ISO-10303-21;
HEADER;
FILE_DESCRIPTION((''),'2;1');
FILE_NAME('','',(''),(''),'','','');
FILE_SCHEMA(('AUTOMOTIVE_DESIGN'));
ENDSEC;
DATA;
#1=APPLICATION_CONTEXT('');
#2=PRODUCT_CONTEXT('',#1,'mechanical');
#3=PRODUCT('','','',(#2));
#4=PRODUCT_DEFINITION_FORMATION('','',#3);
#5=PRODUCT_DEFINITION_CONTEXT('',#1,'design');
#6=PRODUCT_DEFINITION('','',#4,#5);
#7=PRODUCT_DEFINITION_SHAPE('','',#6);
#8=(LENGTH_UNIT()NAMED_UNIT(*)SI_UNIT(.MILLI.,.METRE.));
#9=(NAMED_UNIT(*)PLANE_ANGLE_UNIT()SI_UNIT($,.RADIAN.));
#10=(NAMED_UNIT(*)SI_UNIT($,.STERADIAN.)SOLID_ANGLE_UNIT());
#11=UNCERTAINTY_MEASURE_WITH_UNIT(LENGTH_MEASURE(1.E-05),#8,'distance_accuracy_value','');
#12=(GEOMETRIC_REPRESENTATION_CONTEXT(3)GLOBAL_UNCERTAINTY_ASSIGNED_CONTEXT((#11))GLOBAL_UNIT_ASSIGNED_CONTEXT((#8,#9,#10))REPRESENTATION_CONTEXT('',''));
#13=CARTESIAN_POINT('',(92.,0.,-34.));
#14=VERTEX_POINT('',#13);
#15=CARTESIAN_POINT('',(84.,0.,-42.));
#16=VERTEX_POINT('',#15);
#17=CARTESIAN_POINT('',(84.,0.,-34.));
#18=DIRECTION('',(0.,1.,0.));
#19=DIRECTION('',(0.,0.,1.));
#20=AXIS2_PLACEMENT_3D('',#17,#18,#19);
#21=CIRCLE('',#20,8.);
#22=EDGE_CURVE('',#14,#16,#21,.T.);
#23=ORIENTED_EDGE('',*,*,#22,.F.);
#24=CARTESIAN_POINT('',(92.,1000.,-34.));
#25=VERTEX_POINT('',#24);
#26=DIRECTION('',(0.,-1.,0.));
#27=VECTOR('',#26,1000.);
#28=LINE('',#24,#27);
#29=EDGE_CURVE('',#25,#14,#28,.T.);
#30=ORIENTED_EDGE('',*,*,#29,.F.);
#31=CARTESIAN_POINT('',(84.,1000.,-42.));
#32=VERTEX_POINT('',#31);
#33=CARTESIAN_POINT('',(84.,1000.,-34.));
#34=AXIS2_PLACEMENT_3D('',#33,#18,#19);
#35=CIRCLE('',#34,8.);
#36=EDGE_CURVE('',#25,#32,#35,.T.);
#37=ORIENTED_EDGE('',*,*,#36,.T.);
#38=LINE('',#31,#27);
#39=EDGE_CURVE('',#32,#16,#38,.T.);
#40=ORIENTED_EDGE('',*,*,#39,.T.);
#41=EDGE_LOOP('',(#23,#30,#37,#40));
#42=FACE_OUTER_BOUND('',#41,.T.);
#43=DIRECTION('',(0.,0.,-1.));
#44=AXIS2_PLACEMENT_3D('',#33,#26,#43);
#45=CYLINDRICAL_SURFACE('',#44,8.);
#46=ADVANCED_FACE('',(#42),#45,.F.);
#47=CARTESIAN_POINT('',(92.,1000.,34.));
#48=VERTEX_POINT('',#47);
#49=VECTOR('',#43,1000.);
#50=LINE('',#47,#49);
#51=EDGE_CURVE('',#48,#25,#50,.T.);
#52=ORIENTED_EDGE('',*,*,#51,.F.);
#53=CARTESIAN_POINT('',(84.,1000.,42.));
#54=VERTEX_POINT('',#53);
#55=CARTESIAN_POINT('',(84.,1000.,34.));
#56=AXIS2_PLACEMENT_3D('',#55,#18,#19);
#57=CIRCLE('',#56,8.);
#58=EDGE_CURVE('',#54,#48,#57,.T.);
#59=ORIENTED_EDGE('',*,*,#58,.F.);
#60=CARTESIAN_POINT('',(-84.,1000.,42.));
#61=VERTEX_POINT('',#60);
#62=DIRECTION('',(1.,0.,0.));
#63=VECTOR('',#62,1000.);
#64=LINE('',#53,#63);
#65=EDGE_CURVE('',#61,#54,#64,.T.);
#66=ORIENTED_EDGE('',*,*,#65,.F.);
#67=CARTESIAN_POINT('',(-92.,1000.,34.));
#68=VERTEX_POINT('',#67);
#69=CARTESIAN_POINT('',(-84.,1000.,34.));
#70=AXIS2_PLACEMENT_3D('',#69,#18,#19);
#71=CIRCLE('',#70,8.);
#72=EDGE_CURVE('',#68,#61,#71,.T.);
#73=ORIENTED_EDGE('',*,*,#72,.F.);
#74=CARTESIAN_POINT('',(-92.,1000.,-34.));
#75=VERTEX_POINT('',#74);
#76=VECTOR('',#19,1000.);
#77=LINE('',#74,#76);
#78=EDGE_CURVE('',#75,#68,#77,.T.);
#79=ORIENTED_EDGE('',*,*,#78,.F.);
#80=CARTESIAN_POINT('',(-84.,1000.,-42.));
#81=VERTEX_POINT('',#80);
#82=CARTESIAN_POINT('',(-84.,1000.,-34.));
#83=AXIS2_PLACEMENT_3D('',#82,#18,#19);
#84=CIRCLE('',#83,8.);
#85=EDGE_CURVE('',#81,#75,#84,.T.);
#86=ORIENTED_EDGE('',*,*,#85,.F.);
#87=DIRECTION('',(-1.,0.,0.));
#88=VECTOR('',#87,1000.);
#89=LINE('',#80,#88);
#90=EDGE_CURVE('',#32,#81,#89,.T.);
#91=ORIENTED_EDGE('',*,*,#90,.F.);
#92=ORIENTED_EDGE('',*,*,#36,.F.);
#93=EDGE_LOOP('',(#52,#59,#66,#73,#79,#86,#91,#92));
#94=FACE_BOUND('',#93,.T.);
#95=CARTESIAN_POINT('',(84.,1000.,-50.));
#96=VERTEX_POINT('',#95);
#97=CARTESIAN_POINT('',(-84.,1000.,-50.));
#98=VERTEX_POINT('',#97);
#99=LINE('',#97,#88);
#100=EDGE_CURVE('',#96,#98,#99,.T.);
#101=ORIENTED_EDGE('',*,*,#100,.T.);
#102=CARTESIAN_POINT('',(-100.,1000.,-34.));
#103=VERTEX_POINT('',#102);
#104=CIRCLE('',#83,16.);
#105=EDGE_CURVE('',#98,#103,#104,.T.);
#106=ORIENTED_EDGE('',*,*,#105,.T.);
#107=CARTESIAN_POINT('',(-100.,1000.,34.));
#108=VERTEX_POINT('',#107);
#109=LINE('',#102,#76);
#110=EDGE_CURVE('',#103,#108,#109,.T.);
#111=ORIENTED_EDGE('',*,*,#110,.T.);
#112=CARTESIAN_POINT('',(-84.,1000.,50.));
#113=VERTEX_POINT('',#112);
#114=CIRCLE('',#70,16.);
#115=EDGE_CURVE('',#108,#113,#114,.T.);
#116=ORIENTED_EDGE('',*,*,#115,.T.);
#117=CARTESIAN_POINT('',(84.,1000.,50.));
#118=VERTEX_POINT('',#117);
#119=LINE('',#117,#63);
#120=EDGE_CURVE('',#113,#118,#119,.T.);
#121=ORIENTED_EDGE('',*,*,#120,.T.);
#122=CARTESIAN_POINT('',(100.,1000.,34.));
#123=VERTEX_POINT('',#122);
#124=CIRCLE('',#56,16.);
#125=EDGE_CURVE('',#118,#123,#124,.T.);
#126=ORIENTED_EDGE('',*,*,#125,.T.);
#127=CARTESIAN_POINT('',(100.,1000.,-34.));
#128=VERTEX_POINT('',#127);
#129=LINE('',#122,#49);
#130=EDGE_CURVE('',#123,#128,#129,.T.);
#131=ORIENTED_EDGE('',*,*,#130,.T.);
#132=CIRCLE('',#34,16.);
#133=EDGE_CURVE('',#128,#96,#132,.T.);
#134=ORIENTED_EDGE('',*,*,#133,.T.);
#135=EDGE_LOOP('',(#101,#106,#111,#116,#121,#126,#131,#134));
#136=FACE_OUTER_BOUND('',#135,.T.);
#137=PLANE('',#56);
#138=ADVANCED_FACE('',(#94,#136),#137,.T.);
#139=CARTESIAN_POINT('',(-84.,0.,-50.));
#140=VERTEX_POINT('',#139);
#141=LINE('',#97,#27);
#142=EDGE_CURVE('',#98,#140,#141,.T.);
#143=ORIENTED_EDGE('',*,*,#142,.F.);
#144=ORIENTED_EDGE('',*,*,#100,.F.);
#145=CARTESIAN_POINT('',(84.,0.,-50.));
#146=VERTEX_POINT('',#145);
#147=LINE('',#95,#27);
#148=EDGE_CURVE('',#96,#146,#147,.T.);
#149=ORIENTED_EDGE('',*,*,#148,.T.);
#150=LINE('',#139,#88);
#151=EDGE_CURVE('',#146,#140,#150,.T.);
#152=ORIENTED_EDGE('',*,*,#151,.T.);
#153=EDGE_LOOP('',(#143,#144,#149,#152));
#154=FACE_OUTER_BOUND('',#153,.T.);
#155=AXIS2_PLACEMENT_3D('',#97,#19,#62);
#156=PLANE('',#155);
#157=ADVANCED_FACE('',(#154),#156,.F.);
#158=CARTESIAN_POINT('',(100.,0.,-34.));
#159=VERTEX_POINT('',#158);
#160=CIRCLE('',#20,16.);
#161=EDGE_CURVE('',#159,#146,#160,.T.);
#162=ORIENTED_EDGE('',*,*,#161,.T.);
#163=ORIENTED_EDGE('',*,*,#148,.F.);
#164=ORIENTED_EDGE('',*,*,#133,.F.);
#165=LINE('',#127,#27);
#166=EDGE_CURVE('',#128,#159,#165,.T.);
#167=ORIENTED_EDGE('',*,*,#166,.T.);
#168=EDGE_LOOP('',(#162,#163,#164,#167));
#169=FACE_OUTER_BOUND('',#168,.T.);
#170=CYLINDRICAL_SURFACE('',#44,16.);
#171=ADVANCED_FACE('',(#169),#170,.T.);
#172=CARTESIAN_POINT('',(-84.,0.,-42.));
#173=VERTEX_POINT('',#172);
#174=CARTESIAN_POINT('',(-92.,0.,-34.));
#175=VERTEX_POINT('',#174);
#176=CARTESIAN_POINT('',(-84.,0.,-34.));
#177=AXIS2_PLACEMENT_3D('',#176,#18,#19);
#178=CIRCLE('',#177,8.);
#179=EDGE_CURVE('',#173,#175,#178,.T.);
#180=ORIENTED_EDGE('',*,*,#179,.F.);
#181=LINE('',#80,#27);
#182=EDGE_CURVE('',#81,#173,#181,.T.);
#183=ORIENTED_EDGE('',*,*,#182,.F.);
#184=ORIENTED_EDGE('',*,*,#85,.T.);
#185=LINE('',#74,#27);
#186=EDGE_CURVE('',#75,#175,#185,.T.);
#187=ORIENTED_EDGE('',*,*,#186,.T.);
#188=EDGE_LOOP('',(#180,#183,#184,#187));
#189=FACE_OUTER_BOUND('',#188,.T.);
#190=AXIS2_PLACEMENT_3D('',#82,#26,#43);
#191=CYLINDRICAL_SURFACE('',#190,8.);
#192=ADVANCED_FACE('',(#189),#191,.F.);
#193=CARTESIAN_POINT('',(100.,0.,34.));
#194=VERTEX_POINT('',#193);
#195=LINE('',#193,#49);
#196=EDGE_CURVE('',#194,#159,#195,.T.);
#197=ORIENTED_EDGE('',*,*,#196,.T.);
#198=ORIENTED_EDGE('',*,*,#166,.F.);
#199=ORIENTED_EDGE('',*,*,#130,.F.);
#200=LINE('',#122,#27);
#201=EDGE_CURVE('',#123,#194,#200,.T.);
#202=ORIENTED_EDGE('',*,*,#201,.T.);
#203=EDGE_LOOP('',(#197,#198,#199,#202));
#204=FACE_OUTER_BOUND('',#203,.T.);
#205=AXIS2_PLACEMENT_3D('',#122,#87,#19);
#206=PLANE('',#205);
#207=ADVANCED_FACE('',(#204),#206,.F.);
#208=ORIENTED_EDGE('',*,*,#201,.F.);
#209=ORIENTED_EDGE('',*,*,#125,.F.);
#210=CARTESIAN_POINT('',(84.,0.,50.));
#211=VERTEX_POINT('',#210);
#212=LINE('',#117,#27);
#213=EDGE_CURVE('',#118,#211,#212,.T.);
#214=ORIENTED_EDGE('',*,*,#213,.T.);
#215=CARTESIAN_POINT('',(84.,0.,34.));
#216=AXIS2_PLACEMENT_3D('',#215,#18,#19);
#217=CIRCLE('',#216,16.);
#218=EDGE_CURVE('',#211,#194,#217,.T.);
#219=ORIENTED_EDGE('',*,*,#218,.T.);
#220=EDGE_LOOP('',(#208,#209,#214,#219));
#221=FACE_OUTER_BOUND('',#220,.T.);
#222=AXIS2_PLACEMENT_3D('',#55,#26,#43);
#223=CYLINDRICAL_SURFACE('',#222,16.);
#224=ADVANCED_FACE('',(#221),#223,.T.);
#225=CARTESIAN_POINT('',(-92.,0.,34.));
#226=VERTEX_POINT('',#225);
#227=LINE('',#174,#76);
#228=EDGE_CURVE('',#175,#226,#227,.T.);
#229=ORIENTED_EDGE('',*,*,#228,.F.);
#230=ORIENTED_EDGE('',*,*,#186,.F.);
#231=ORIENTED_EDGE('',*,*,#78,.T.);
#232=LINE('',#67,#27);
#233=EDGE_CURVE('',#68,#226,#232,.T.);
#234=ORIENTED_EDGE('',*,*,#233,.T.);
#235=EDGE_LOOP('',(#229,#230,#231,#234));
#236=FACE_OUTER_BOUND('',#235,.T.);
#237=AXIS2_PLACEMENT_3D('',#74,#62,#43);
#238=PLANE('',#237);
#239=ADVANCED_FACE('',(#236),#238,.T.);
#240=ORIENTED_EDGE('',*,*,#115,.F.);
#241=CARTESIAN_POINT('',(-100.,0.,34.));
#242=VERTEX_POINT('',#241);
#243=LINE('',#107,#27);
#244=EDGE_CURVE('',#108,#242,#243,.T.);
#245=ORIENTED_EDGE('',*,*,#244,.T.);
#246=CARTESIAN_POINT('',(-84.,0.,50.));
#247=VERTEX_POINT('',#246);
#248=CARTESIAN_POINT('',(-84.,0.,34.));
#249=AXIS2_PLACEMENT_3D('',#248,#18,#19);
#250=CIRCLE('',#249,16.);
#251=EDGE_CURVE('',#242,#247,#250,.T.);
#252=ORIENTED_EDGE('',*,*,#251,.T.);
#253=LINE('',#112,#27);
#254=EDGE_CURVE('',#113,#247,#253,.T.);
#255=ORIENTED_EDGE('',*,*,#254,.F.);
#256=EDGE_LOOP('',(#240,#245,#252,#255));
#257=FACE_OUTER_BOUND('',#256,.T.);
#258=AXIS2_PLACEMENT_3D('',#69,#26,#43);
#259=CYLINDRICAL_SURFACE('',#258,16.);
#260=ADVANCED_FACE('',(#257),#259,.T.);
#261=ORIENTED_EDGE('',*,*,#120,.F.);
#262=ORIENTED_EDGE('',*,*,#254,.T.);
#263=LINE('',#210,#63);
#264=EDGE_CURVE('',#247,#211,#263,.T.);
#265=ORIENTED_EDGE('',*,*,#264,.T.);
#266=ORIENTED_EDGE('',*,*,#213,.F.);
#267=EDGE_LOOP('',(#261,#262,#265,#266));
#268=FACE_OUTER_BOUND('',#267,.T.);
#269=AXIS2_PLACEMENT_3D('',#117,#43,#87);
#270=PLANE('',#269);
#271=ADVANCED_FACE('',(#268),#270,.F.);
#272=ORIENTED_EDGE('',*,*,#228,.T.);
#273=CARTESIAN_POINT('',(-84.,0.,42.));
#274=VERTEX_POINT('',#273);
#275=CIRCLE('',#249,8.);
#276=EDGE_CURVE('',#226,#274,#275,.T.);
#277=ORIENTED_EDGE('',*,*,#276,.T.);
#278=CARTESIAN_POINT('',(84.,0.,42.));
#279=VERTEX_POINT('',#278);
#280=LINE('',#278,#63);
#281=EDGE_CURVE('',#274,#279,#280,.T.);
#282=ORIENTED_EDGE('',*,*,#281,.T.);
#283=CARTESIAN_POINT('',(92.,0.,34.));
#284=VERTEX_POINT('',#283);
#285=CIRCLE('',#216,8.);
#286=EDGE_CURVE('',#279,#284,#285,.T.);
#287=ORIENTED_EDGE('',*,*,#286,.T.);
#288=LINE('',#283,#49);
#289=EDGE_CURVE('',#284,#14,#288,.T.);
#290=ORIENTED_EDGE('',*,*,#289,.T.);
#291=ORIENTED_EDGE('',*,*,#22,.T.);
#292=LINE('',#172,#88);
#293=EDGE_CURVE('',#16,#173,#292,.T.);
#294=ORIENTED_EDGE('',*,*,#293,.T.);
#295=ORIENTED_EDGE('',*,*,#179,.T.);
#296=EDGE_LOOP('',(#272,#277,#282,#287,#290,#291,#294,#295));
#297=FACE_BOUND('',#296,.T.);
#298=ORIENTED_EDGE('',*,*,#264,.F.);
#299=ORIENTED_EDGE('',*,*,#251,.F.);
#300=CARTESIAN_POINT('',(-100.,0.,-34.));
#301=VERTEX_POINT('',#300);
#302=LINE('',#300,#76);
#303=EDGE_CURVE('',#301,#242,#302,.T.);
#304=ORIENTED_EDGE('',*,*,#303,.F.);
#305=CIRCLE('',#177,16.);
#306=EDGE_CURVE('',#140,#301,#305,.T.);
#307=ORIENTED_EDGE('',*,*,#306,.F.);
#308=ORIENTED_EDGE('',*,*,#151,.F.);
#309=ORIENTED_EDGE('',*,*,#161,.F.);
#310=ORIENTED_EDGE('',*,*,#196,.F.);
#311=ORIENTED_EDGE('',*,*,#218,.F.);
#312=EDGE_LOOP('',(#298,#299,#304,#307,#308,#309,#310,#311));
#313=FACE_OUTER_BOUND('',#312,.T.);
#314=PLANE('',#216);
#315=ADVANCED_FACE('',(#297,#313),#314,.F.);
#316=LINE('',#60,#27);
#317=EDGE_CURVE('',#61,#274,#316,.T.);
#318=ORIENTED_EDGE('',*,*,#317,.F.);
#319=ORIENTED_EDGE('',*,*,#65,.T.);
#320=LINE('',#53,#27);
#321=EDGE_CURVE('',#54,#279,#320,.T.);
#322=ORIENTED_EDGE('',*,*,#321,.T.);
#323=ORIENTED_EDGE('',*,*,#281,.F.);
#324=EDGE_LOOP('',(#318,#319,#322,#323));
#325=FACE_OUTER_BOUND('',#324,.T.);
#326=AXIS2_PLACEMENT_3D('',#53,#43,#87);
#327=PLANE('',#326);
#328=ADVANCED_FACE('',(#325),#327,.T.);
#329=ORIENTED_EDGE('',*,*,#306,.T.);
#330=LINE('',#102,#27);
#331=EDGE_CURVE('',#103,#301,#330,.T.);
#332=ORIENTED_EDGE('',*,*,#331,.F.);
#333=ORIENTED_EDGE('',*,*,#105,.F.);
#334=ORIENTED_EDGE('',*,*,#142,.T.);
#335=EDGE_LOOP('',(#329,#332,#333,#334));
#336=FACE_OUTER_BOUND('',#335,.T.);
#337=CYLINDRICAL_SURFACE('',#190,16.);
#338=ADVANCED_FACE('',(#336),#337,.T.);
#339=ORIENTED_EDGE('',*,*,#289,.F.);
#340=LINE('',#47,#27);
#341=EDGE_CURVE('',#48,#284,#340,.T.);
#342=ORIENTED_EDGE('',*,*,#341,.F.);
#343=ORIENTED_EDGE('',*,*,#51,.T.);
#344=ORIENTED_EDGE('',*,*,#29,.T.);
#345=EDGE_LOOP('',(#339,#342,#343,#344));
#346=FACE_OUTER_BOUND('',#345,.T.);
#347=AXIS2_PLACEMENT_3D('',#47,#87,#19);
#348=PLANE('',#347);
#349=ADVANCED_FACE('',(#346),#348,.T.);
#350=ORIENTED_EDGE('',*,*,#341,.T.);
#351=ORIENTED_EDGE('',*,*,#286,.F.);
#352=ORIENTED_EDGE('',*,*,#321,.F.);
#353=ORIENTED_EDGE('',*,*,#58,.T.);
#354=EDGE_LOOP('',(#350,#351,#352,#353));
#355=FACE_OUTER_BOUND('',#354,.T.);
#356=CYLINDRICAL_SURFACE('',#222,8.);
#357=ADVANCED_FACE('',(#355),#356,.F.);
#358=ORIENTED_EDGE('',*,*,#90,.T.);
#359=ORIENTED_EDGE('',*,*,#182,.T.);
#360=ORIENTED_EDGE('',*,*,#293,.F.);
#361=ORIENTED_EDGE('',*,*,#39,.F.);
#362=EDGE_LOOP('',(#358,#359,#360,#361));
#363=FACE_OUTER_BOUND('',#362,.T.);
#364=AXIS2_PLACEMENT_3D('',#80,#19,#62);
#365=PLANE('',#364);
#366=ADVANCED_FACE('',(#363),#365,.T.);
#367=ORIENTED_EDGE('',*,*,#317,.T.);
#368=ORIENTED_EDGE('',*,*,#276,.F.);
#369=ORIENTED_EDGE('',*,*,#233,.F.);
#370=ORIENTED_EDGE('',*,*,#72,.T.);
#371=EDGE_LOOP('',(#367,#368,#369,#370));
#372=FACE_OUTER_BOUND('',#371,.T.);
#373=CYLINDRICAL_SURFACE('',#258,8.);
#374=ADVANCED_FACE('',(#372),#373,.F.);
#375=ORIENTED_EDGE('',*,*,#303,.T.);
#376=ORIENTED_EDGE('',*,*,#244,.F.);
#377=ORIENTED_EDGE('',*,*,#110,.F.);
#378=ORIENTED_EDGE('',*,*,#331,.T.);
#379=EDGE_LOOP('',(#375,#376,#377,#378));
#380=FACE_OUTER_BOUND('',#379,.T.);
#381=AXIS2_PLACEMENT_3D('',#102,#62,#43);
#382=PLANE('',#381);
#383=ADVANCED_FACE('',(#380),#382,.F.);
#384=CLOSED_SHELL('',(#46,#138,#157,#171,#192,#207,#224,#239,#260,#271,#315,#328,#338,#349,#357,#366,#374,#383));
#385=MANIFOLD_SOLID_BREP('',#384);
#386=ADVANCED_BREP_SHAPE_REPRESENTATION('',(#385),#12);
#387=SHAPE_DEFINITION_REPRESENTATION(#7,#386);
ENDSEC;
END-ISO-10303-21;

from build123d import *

# Parameters (mm, degrees)
GB_T_6728_2002_RECTANGULAR_HOLLOW_SECTIO_DEPTH = 1000


with BuildPart() as part:
    # Sketch12 → GB/T 6728-2002 rectangular hollow section 200X100X8(2) (new body)
    with BuildSketch(Plane.ZX):
        with BuildLine():
            Line((-34, -100), (34, -100))
            ThreePointArc((34, -100), (45.313708499, -95.313708499), (50, -84))
            Line((50, -84), (50, 84))
            ThreePointArc((50, 84), (45.313708499, 95.313708499), (34, 100))
            Line((34, 100), (-34, 100))
            ThreePointArc((-34, 100), (-45.313708499, 95.313708499), (-50, 84))
            Line((-50, 84), (-50, -84))
            ThreePointArc((-50, -84), (-45.313708499, -95.313708499), (-34, -100))
        make_face()
        with BuildLine():
            Line((-34, -92), (34, -92))
            ThreePointArc((34, -92), (39.656854249, -89.656854249), (42, -84))
            Line((42, -84), (42, 84))
            ThreePointArc((42, 84), (39.656854249, 89.656854249), (34, 92))
            Line((34, 92), (-34, 92))
            ThreePointArc((-34, 92), (-39.656854249, 89.656854249), (-42, 84))
            Line((-42, 84), (-42, -84))
            ThreePointArc((-42, -84), (-39.656854249, -89.656854249), (-34, -92))
        make_face(mode=Mode.SUBTRACT)
    extrude(amount=GB_T_6728_2002_RECTANGULAR_HOLLOW_SECTIO_DEPTH)


solid = part.part
